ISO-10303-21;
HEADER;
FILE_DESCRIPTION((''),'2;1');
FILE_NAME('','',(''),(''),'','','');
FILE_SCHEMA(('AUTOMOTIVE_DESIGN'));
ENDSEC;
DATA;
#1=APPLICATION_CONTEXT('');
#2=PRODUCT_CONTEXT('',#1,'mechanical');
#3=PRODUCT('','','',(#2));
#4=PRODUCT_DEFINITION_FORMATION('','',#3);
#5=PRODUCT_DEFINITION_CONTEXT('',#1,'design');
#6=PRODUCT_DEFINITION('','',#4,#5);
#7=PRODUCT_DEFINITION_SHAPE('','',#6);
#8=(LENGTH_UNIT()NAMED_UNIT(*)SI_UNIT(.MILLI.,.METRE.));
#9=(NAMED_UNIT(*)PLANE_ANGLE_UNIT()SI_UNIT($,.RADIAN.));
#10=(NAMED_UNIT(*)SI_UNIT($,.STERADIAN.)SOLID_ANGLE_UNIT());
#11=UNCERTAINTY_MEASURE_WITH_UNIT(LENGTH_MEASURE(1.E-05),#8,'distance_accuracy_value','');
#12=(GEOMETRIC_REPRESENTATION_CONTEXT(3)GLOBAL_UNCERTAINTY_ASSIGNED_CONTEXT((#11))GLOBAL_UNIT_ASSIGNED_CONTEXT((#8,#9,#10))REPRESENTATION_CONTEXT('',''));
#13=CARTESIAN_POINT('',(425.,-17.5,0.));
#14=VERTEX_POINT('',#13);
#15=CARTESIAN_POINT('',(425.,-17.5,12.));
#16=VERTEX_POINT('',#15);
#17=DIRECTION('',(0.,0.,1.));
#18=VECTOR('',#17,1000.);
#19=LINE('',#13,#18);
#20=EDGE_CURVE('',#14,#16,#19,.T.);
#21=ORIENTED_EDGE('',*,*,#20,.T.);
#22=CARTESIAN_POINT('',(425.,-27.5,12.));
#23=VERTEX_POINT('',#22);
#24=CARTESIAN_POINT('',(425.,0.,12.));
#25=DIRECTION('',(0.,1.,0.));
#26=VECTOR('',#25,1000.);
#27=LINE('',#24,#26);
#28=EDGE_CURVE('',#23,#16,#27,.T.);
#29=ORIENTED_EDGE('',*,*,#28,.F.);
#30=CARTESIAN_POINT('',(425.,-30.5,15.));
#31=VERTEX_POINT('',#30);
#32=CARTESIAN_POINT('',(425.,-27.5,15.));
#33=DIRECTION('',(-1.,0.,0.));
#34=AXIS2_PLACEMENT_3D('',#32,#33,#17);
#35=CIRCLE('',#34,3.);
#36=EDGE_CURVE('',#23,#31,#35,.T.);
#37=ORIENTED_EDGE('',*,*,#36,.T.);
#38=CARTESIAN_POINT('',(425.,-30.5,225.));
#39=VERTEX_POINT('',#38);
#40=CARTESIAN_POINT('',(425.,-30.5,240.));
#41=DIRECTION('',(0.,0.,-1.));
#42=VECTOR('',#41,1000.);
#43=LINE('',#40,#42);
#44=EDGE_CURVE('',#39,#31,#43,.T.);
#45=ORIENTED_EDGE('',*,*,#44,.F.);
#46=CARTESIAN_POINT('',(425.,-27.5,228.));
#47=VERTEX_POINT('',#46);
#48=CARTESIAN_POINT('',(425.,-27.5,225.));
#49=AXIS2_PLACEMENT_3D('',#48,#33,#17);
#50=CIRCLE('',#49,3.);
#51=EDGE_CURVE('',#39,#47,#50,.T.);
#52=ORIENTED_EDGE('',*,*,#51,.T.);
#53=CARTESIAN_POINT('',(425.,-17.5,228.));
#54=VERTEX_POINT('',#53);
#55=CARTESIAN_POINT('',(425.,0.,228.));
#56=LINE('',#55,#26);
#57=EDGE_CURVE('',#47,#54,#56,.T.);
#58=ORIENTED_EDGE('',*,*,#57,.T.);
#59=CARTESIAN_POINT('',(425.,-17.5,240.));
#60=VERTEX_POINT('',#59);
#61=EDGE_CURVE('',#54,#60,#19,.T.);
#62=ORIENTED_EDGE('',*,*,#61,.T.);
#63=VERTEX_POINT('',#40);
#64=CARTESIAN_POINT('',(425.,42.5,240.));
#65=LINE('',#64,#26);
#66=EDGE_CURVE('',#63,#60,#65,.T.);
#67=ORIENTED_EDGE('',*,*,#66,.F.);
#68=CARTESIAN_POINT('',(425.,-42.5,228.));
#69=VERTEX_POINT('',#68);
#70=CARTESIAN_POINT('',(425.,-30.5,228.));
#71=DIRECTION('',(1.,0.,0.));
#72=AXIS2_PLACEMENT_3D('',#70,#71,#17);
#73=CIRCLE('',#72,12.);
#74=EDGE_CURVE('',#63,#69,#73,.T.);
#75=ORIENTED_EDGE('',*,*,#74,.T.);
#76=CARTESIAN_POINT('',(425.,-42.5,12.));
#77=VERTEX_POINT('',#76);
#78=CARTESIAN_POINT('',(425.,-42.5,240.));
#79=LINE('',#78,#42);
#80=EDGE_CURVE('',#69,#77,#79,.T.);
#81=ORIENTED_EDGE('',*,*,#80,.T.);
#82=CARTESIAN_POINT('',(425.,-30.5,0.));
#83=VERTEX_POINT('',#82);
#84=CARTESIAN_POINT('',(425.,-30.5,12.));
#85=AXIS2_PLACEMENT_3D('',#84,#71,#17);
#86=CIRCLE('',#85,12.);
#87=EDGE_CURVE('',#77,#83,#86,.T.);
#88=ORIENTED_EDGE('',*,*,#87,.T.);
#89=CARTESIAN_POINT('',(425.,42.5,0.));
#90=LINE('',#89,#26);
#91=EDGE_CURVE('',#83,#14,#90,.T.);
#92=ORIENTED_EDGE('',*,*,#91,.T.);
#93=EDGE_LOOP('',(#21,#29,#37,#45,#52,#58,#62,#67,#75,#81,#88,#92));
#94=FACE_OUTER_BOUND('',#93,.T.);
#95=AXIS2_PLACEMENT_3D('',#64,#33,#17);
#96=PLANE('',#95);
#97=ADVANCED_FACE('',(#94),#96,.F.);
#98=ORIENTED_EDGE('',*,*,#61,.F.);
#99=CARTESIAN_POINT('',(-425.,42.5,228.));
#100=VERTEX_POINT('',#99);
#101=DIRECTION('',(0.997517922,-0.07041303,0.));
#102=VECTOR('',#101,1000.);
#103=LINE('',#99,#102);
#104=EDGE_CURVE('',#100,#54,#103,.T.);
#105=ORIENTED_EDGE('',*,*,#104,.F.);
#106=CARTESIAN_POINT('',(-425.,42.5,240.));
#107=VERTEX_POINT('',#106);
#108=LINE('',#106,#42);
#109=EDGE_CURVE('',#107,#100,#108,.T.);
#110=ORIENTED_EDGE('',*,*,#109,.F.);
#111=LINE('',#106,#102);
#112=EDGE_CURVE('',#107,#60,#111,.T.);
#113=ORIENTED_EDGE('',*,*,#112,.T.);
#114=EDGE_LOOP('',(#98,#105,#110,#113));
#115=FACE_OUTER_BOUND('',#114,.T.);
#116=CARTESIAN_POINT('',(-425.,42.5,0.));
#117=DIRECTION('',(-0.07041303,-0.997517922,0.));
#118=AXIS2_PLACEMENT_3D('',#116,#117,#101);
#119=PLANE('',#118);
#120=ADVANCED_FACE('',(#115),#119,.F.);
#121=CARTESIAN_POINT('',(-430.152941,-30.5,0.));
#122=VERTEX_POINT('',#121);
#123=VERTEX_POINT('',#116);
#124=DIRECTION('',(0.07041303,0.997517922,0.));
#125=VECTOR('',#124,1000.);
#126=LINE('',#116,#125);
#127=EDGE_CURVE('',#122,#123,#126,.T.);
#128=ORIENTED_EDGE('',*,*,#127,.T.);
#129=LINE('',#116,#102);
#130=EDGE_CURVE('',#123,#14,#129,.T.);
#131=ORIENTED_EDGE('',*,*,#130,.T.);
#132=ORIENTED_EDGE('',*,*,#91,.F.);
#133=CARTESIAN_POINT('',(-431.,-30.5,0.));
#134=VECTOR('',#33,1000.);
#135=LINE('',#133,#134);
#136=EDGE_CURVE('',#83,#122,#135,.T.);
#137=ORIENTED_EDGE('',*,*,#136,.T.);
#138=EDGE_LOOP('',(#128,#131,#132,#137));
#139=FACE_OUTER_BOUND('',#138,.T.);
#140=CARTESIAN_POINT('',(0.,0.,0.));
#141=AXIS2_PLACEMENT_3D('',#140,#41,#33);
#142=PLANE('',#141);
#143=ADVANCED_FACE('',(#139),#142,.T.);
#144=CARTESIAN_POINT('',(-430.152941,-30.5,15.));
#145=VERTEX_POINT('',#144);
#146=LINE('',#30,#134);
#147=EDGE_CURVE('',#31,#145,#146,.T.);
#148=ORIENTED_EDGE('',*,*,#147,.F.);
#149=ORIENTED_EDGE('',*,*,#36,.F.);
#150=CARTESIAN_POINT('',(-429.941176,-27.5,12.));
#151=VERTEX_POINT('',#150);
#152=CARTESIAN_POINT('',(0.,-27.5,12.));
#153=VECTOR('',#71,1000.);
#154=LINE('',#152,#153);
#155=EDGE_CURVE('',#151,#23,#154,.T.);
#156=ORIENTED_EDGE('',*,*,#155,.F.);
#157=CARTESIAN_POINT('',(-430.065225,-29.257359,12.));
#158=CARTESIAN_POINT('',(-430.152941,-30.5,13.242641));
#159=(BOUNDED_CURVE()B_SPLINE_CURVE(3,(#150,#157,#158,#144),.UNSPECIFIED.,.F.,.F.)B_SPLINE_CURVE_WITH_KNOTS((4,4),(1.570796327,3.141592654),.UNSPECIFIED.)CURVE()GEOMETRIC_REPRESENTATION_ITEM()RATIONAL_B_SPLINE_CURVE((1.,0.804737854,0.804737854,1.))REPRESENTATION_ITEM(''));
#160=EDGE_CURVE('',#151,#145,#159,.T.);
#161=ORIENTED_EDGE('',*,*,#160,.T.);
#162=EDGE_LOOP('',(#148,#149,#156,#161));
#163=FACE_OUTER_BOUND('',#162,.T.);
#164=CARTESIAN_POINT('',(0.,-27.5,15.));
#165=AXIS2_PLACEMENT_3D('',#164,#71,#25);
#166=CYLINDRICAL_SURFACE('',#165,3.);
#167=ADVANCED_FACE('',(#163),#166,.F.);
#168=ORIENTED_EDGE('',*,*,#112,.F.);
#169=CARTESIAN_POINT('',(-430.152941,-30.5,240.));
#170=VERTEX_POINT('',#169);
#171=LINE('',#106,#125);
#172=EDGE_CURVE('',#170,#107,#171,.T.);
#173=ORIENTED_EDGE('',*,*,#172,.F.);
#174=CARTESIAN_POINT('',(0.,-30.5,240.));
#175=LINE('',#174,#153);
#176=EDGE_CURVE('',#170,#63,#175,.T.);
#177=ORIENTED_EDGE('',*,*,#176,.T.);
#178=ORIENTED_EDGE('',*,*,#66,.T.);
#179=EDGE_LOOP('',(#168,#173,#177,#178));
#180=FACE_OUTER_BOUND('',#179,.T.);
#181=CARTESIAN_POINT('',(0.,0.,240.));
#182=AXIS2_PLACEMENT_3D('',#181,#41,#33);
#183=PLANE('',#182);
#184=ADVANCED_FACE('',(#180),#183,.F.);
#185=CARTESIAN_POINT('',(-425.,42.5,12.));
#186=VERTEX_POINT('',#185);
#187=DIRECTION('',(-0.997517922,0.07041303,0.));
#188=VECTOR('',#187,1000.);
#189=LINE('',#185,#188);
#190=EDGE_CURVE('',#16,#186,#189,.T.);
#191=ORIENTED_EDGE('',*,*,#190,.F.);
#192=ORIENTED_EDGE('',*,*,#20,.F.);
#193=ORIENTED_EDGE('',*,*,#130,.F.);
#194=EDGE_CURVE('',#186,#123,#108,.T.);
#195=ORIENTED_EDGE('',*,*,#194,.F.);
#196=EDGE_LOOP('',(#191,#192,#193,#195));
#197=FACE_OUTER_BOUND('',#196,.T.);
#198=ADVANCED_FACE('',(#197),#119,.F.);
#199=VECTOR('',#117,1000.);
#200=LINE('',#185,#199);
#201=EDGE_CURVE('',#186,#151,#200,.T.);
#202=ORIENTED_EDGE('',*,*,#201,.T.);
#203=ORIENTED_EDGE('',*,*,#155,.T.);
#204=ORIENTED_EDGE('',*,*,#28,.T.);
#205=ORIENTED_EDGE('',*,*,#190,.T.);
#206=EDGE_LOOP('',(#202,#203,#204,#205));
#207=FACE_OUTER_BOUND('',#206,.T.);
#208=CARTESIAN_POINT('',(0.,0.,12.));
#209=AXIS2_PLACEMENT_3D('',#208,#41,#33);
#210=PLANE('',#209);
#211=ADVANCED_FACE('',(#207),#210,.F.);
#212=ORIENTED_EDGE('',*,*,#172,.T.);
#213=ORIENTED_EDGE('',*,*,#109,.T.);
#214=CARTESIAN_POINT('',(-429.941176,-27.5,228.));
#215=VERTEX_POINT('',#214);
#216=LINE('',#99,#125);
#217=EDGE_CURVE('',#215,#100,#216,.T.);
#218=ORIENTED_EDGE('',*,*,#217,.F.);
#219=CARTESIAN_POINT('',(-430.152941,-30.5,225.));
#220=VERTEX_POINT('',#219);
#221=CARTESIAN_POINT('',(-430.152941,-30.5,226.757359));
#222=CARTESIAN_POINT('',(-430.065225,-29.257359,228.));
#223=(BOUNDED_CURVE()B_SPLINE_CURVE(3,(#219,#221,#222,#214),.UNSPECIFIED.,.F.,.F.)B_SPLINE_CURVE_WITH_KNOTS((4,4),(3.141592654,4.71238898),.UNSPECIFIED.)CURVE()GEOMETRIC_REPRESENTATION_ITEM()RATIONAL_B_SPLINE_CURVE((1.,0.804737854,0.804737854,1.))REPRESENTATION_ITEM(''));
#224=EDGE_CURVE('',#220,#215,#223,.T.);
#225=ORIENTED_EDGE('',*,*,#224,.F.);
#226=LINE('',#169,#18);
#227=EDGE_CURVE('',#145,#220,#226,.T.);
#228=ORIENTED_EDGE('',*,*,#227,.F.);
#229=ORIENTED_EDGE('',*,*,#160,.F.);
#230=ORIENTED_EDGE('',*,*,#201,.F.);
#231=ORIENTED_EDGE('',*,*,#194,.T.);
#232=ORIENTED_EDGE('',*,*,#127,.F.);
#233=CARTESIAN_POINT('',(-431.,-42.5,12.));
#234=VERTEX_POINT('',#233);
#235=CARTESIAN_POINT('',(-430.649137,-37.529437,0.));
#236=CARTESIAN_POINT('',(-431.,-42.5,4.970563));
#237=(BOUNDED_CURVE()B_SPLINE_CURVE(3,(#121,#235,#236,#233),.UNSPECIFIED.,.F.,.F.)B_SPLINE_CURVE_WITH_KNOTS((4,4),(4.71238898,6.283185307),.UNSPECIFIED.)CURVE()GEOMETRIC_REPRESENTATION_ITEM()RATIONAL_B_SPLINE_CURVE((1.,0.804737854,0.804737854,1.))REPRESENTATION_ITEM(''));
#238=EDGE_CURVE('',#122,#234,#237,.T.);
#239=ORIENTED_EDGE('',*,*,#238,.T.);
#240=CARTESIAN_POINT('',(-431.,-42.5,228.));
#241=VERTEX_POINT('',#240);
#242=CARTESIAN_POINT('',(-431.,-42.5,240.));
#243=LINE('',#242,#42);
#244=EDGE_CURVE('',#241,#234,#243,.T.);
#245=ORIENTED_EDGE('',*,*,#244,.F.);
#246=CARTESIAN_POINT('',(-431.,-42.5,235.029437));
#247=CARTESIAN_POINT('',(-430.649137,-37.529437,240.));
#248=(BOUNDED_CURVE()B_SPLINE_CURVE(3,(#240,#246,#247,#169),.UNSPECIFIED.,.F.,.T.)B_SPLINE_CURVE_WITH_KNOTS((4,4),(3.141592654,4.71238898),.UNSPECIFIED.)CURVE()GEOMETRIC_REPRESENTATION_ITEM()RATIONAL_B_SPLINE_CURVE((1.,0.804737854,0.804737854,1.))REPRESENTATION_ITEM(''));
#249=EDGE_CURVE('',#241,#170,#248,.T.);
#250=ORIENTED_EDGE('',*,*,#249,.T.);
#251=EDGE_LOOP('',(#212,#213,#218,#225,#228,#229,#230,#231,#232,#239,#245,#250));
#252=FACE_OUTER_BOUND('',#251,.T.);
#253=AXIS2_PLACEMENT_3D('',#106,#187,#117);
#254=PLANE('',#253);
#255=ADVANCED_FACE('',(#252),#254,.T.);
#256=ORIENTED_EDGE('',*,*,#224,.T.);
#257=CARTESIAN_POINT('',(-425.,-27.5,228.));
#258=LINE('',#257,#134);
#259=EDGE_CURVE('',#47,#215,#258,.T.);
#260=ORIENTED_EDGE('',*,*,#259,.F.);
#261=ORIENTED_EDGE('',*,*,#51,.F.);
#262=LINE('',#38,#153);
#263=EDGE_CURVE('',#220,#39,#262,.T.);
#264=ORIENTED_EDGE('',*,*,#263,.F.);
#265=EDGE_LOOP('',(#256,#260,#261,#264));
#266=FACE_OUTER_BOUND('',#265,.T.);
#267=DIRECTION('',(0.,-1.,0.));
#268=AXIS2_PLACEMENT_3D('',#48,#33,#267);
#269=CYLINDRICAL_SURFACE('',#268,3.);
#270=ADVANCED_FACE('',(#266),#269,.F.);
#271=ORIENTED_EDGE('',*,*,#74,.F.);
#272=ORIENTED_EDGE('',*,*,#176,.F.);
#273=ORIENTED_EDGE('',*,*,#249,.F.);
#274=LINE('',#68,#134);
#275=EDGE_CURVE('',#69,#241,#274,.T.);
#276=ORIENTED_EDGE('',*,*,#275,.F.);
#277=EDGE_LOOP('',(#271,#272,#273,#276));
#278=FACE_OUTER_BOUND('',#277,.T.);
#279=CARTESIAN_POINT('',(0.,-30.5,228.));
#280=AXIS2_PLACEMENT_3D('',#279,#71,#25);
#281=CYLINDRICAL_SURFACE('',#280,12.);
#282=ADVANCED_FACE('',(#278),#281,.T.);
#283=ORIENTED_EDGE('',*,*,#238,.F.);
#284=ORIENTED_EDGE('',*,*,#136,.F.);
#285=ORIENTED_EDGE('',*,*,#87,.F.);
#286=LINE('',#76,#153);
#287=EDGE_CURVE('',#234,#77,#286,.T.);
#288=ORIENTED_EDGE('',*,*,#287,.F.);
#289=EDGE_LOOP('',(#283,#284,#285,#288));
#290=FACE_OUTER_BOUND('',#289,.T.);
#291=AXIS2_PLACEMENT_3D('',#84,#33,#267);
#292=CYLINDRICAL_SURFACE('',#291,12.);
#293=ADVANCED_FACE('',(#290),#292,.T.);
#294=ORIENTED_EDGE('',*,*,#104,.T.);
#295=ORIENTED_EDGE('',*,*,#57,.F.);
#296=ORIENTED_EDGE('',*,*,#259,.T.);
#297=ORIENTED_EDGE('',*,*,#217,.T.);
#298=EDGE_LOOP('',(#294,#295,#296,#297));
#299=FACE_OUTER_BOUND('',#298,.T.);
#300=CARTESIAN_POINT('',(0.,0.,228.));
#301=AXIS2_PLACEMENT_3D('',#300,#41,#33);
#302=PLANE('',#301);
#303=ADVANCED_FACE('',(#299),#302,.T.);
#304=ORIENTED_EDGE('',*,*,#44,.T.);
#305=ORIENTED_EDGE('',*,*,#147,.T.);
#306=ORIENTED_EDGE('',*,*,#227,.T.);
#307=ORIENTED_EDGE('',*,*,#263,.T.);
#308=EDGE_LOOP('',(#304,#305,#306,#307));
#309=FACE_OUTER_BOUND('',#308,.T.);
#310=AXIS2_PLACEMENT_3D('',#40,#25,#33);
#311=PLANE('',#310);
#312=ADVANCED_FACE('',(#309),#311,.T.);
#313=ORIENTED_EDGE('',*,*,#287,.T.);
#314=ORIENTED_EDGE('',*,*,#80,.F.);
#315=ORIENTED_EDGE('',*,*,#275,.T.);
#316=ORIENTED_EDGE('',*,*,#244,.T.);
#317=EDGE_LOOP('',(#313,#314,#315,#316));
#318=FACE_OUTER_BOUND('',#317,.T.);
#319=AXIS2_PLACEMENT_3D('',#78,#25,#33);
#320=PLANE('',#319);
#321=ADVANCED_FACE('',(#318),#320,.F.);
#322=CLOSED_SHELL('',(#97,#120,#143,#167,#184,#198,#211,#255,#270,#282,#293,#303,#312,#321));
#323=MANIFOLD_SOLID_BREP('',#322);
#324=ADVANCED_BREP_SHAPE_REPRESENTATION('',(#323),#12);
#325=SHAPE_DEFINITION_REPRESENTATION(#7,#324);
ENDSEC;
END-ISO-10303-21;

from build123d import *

# Parameters (mm, degrees)
SKETCH_1_W          = 850
SKETCH_1_H          = 85
EXTRUDE_1_DEPTH     = 240
CUT_EXTRUDE_1_DEPTH = 240
SHELL_1_T           = -12
EXTRUDE_2_DEPTH     = 240
SKETCH_5_W          = 850
SKETCH_5_H          = 216
CUT_EXTRUDE_3_DEPTH = 94
FILLET_1_R          = 12
FILLET_2_R          = 3
CUT_EXTRUDE_4_DEPTH = 240


with BuildPart() as part:
    # 草图1 → 凸台-拉伸1 (new body)
    with BuildSketch(Plane.XY):
        Rectangle(SKETCH_1_W, SKETCH_1_H)
    extrude(amount=EXTRUDE_1_DEPTH)

    # 草图2 → 切除-拉伸1 (cut)
    with BuildSketch(Plane.XY.offset(240)):
        Polygon((-425, 42.5), (425, -17.5), (425, 42.5), align=None)
    extrude(amount=-CUT_EXTRUDE_1_DEPTH, mode=Mode.SUBTRACT)

    # 抽壳1
    shell_1_openings = [part.faces().sort_by_distance(p)[0] for p in [
        (425, -30, 120),
        (-425, 0, 120),
    ]]
    offset(amount=SHELL_1_T, openings=shell_1_openings, kind=Kind.INTERSECTION)

    # 草图6 → 凸台-拉伸2 (add)
    with BuildSketch(Plane(origin=(0, 0, 0), x_dir=(-1, 0, 0), z_dir=(0, 0, -1))):
        Polygon((425, 42.5), (431, -42.5), (425, -42.5), align=None)
    extrude(amount=-EXTRUDE_2_DEPTH)

    # 草图5 → 切除-拉伸3 (cut)
    with BuildSketch(Plane(origin=(0, -30.5, 0), x_dir=(1, 0, 0), z_dir=(0, 1, 0))):
        with Locations((0, -120)):
            Rectangle(SKETCH_5_W, SKETCH_5_H)
    extrude(amount=CUT_EXTRUDE_3_DEPTH, mode=Mode.SUBTRACT)

    # 圆角1
    fillet_1_edges = [part.edges().sort_by_distance(p)[0] for p in [
        (-3, -42.5, 0),
        (-3, -42.5, 240),
    ]]
    fillet(fillet_1_edges, radius=FILLET_1_R)

    # 圆角2
    fillet_2_edges = [part.edges().sort_by_distance(p)[0] for p in [
        (0, -30.5, 12),
        (0, -30.5, 228),
    ]]
    fillet(fillet_2_edges, radius=FILLET_2_R)

    # 草图7 → 切除-拉伸4 (cut)
    with BuildSketch(Plane(origin=(-425, 0, 0), x_dir=(0, 0, -1), z_dir=(1, 0, 0))):
        with BuildLine():
            Line((-225, -30.5), (-15, -30.5))
            ThreePointArc((-15, -30.5), (-12.878679656, -29.621320344), (-12, -27.5))
            Line((-12, -27.5), (-12, 42.5))
            Line((-12, 42.5), (-228, 42.5))
            Line((-228, 42.5), (-228, -27.5))
            ThreePointArc((-228, -27.5), (-227.121320344, -29.621320344), (-225, -30.5))
        make_face()
    extrude(amount=-CUT_EXTRUDE_4_DEPTH, mode=Mode.SUBTRACT)


solid = part.part
